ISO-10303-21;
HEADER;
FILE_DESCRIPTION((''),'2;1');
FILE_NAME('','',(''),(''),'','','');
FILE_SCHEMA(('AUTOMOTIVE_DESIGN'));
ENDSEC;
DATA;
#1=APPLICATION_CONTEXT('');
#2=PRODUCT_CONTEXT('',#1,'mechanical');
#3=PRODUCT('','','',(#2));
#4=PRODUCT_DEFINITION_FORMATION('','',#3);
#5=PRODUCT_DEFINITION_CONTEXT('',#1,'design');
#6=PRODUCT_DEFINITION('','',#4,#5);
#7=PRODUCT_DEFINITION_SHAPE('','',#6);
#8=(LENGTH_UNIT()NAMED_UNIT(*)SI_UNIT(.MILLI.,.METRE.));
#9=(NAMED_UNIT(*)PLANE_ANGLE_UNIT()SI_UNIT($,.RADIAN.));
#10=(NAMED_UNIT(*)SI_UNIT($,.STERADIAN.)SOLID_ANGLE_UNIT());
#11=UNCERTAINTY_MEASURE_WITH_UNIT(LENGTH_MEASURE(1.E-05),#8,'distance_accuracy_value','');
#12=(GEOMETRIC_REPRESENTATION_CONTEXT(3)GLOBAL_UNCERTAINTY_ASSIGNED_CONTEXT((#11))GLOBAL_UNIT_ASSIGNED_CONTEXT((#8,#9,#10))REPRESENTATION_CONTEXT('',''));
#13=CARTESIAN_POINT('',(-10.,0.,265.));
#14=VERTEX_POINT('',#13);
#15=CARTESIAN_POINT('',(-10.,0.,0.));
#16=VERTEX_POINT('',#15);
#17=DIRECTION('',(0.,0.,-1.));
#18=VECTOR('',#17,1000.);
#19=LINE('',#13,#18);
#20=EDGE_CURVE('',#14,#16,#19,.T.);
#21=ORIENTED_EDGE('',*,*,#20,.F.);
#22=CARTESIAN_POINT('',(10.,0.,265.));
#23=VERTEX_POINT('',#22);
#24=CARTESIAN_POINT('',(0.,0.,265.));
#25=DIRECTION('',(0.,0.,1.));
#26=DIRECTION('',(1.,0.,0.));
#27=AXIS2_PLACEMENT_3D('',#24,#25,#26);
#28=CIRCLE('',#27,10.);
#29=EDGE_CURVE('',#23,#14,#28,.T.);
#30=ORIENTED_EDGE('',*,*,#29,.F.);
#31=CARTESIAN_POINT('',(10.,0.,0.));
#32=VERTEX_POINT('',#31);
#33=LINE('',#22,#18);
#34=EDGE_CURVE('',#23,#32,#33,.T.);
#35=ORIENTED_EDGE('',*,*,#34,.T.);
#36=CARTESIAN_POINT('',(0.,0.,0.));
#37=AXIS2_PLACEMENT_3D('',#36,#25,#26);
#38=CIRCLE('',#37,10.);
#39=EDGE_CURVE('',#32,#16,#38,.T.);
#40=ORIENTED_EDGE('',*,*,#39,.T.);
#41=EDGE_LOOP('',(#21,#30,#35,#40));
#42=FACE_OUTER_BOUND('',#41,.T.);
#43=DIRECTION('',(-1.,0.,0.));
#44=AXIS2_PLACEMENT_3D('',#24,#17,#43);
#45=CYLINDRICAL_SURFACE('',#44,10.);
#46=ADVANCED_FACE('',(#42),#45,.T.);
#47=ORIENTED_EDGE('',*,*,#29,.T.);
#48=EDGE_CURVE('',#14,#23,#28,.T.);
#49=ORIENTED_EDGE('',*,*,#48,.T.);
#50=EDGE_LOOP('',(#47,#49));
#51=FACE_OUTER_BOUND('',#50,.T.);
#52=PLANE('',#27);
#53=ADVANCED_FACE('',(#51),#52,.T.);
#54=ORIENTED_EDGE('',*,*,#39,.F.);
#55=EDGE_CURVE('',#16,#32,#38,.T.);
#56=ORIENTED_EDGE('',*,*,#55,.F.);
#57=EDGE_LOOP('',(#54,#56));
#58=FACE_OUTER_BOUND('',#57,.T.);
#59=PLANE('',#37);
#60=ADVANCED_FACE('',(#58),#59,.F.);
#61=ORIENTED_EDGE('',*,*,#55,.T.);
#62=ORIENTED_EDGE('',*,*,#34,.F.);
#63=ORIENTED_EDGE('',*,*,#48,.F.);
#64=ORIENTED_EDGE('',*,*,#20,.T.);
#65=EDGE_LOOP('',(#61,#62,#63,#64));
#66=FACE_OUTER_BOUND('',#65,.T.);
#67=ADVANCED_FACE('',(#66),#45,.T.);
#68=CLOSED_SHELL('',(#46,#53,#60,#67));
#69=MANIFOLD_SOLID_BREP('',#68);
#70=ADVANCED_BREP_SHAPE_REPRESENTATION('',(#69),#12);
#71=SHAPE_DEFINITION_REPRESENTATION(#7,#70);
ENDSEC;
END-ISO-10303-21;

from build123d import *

# Parameters (mm, degrees)
SKETCH_1_R      = 10
EXTRUDE_1_DEPTH = 265


with BuildPart() as part:
    # 草图1 → 凸台-拉伸1 (new body)
    with BuildSketch(Plane.XY):
        Circle(SKETCH_1_R)
    extrude(amount=EXTRUDE_1_DEPTH)


solid = part.part
